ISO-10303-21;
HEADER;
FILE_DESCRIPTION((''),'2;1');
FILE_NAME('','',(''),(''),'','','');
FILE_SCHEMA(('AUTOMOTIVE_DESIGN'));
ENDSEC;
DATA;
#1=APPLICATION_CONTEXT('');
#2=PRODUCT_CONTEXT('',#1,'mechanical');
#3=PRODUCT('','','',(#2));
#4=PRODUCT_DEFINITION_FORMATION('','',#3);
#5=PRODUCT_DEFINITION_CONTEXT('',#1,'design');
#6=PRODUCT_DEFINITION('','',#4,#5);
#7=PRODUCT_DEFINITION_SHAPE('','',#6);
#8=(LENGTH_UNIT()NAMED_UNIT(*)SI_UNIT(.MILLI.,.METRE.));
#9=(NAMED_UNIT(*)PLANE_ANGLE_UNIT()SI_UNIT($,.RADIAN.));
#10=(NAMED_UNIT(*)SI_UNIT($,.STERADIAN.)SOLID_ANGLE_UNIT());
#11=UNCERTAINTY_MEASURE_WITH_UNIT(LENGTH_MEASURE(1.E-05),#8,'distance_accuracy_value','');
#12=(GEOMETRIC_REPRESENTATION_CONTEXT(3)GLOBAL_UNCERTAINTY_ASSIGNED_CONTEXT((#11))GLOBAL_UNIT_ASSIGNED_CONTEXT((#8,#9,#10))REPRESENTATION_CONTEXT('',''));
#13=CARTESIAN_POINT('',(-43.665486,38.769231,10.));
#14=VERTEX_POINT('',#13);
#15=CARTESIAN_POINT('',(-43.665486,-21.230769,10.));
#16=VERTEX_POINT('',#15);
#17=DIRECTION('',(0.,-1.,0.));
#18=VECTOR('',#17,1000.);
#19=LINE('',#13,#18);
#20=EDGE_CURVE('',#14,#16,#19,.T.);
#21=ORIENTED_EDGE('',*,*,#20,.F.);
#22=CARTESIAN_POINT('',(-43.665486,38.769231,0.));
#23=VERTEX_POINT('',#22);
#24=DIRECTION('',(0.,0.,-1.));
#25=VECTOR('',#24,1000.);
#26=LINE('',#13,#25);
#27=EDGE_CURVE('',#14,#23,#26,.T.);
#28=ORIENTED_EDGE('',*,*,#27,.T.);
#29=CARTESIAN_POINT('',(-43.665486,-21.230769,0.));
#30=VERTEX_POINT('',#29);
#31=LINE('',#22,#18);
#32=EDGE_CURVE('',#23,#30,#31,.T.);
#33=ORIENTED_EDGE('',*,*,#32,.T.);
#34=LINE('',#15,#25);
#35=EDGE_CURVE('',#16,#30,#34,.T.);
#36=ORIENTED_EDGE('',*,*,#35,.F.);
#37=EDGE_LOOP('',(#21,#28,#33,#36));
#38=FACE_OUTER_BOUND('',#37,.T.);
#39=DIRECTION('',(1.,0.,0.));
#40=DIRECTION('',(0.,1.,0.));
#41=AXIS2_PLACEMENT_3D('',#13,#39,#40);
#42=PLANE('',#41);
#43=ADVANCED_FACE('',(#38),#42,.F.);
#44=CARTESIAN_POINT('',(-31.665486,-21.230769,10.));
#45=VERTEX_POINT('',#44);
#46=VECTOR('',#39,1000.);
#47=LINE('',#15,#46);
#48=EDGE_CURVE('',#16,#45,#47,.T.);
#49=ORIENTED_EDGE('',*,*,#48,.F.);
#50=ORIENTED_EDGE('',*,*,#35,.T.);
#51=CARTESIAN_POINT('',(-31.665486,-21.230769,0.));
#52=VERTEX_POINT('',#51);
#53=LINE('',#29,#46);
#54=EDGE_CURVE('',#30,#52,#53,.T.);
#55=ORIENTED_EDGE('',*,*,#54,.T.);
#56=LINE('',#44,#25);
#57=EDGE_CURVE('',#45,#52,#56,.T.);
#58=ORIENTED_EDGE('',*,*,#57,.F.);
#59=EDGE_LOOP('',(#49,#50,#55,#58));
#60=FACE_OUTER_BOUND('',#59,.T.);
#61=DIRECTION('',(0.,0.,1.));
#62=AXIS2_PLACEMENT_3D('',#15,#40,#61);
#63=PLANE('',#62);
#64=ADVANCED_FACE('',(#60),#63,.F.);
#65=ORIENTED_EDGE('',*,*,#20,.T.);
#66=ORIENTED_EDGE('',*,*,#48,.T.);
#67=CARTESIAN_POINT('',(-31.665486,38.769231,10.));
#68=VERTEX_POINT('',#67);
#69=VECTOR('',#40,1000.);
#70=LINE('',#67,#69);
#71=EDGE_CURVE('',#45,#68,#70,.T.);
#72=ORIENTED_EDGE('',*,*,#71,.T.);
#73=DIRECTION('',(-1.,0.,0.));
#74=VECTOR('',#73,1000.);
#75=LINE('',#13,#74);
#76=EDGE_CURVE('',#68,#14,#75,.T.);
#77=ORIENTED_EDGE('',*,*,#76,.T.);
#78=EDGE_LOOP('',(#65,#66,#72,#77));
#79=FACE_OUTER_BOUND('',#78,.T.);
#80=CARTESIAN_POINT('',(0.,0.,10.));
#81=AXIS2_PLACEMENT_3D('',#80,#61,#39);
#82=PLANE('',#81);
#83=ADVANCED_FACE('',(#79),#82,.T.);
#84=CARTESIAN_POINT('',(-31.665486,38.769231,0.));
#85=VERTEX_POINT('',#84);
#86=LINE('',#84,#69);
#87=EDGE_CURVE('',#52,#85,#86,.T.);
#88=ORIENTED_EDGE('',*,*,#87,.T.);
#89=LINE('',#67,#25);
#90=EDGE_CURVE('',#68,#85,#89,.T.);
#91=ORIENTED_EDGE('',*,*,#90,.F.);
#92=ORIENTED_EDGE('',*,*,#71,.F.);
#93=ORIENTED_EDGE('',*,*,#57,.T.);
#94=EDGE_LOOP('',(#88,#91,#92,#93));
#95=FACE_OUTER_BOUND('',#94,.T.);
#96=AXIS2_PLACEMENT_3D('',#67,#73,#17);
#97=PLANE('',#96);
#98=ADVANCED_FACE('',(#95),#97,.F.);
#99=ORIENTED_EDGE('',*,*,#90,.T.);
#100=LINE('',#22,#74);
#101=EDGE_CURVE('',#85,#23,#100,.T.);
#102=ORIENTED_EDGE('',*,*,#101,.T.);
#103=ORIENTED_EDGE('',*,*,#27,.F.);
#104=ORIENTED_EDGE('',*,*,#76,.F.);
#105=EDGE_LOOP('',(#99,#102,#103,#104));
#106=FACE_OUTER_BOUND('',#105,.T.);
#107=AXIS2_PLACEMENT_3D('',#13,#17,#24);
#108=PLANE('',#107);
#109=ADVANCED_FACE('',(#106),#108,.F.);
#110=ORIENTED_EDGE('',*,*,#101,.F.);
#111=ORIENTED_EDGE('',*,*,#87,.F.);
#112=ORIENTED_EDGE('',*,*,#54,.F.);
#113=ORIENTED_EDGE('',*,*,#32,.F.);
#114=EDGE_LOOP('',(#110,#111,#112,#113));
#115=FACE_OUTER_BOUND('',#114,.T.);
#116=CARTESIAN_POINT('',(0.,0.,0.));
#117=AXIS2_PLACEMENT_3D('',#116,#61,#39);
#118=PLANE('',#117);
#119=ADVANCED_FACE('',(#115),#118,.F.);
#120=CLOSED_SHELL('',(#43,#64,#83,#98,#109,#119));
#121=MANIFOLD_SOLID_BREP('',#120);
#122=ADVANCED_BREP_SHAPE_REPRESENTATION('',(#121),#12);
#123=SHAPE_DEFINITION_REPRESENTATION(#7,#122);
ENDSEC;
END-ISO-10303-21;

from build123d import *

# Parameters (mm, degrees)
SKETCH1_W           = 12
SKETCH1_H           = 60
BOSS_EXTRUDE1_DEPTH = 10


with BuildPart() as part:
    # Sketch1 → Boss-Extrude1 (new body)
    with BuildSketch(Plane.XY):
        with Locations((-37.66548583, 8.769230769)):
            Rectangle(SKETCH1_W, SKETCH1_H)
    extrude(amount=BOSS_EXTRUDE1_DEPTH)


solid = part.part
